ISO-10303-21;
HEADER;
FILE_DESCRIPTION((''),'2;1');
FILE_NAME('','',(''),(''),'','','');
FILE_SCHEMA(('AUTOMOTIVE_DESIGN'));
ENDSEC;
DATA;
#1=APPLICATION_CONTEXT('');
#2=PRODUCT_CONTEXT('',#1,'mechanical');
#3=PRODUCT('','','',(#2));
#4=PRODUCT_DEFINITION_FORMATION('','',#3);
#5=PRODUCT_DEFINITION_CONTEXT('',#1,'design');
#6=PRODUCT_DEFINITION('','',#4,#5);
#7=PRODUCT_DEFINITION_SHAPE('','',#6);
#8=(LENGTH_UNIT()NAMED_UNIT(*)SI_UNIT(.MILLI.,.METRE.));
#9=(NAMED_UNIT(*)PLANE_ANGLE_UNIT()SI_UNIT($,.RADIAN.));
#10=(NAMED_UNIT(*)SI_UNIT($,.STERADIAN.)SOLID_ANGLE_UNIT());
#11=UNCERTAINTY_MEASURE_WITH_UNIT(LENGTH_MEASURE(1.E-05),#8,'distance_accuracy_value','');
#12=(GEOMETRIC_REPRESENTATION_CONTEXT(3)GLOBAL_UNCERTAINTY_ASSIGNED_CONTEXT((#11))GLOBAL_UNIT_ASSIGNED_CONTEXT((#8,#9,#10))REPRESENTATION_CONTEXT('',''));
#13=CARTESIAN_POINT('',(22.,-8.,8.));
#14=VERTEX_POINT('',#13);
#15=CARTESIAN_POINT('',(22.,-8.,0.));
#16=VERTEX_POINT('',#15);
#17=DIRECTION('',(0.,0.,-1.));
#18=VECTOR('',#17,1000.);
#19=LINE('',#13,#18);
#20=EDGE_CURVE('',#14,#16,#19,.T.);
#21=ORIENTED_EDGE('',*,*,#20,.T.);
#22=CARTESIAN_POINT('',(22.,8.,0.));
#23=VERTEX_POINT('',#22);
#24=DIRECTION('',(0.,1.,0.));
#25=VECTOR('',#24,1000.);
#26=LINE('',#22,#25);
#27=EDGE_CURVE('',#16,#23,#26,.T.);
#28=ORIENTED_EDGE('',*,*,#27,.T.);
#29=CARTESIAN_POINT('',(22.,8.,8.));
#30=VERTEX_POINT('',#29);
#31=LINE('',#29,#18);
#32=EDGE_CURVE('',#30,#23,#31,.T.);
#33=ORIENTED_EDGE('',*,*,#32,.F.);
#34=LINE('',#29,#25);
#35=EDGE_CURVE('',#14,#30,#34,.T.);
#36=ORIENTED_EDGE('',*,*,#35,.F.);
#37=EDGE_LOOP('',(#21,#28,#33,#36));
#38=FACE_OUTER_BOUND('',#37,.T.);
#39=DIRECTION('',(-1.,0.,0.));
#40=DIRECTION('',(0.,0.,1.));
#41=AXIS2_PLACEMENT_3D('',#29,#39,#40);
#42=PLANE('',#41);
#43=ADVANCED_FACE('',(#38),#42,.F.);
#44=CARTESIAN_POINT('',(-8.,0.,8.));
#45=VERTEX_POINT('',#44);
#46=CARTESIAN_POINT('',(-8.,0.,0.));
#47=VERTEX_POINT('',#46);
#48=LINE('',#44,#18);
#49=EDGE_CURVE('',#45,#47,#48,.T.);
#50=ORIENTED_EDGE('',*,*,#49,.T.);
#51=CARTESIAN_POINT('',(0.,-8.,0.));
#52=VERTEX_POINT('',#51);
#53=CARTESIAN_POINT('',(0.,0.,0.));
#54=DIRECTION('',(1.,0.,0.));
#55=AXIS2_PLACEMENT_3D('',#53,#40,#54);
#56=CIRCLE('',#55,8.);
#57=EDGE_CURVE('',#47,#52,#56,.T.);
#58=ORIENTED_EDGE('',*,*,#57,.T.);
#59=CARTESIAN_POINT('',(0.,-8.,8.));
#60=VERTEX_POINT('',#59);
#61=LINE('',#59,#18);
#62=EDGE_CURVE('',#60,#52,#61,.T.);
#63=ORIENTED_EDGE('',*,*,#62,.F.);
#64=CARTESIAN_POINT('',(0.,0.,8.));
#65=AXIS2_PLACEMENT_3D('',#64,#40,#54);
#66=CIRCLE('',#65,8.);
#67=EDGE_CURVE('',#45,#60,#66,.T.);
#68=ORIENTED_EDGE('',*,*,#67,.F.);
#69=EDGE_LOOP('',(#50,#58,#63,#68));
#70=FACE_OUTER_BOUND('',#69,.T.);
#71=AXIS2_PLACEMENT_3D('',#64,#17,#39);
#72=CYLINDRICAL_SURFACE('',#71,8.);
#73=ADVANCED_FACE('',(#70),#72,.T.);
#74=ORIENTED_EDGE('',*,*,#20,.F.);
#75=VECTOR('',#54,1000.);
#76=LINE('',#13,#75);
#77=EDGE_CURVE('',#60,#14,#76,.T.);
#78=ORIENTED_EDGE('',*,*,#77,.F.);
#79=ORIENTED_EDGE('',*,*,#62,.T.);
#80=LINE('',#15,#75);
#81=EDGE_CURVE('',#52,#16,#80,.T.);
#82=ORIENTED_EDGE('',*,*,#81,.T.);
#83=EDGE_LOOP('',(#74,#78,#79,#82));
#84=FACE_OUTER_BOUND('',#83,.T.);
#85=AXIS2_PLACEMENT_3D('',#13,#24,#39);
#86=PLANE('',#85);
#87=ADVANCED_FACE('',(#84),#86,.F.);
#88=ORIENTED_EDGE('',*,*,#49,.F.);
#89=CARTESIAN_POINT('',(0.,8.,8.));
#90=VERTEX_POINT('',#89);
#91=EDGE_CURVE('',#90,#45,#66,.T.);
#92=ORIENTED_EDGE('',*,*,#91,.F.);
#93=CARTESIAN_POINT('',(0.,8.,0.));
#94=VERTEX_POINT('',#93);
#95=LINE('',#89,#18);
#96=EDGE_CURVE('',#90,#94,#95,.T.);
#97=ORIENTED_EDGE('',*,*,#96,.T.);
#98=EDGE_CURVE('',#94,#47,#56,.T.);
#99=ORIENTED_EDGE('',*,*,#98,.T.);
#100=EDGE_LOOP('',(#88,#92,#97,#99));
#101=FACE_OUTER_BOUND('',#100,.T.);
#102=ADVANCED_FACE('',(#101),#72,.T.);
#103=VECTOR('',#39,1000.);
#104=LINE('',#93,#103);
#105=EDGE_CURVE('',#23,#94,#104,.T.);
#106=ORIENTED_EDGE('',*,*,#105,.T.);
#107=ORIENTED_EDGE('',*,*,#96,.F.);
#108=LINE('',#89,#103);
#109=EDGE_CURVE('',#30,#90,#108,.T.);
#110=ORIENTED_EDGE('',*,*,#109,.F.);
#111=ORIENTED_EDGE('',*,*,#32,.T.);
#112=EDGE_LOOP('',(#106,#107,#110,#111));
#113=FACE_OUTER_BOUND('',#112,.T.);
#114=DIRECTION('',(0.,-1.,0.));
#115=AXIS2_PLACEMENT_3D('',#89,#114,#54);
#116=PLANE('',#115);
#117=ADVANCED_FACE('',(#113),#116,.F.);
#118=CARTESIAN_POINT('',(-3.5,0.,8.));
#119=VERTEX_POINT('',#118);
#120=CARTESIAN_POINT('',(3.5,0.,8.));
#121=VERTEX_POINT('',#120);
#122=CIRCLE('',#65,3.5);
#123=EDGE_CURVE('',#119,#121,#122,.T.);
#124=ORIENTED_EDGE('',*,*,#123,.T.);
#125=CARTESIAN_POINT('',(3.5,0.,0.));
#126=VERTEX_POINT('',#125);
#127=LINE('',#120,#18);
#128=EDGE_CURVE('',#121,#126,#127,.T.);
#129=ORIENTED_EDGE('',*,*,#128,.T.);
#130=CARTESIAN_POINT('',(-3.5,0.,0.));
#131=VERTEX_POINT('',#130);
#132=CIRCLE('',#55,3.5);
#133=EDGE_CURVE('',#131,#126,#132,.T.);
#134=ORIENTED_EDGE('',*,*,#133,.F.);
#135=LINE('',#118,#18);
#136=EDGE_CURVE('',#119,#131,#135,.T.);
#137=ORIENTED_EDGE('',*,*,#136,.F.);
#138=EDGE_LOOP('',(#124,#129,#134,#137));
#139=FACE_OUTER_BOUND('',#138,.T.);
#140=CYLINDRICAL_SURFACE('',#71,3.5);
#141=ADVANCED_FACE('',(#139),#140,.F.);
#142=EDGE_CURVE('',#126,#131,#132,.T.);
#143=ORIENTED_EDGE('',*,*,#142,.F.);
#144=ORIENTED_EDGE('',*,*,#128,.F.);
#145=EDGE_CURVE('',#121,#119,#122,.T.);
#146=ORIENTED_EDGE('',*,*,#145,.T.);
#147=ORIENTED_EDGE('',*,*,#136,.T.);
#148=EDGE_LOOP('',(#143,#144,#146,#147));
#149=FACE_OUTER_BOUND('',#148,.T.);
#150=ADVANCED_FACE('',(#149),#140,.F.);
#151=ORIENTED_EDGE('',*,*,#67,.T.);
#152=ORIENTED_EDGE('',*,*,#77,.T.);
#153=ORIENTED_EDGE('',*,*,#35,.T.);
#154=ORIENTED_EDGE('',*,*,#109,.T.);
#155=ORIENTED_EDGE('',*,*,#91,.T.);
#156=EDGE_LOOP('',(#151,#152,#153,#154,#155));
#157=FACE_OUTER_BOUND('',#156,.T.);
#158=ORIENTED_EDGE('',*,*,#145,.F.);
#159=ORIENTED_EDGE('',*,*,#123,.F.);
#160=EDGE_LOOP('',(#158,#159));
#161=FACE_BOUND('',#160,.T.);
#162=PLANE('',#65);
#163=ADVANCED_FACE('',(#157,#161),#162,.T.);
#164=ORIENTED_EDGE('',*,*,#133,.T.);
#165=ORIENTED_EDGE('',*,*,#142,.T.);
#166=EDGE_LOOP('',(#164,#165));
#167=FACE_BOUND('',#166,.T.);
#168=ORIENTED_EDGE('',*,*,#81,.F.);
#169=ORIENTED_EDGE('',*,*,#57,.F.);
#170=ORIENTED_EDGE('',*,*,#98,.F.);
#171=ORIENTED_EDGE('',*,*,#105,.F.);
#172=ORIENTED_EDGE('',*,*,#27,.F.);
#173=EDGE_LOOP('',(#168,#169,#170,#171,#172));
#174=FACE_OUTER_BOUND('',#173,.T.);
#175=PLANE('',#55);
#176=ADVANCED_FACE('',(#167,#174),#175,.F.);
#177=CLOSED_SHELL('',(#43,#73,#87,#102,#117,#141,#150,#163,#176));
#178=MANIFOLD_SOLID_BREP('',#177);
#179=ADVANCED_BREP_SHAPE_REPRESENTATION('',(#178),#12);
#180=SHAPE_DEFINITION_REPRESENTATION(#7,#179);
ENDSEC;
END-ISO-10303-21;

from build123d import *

# Parameters (mm, degrees)
SKETCH1_R           = 3.5
BOSS_EXTRUDE1_DEPTH = 8


with BuildPart() as part:
    # Sketch1 → Boss-Extrude1 (new body)
    with BuildSketch(Plane.XY):
        with BuildLine():
            Line((0, 8), (22, 8))
            Line((22, 8), (22, -8))
            Line((22, -8), (0, -8))
            ThreePointArc((0, -8), (-8, 0), (0, 8))
        make_face()
        Circle(SKETCH1_R, mode=Mode.SUBTRACT)
    extrude(amount=BOSS_EXTRUDE1_DEPTH)


solid = part.part
